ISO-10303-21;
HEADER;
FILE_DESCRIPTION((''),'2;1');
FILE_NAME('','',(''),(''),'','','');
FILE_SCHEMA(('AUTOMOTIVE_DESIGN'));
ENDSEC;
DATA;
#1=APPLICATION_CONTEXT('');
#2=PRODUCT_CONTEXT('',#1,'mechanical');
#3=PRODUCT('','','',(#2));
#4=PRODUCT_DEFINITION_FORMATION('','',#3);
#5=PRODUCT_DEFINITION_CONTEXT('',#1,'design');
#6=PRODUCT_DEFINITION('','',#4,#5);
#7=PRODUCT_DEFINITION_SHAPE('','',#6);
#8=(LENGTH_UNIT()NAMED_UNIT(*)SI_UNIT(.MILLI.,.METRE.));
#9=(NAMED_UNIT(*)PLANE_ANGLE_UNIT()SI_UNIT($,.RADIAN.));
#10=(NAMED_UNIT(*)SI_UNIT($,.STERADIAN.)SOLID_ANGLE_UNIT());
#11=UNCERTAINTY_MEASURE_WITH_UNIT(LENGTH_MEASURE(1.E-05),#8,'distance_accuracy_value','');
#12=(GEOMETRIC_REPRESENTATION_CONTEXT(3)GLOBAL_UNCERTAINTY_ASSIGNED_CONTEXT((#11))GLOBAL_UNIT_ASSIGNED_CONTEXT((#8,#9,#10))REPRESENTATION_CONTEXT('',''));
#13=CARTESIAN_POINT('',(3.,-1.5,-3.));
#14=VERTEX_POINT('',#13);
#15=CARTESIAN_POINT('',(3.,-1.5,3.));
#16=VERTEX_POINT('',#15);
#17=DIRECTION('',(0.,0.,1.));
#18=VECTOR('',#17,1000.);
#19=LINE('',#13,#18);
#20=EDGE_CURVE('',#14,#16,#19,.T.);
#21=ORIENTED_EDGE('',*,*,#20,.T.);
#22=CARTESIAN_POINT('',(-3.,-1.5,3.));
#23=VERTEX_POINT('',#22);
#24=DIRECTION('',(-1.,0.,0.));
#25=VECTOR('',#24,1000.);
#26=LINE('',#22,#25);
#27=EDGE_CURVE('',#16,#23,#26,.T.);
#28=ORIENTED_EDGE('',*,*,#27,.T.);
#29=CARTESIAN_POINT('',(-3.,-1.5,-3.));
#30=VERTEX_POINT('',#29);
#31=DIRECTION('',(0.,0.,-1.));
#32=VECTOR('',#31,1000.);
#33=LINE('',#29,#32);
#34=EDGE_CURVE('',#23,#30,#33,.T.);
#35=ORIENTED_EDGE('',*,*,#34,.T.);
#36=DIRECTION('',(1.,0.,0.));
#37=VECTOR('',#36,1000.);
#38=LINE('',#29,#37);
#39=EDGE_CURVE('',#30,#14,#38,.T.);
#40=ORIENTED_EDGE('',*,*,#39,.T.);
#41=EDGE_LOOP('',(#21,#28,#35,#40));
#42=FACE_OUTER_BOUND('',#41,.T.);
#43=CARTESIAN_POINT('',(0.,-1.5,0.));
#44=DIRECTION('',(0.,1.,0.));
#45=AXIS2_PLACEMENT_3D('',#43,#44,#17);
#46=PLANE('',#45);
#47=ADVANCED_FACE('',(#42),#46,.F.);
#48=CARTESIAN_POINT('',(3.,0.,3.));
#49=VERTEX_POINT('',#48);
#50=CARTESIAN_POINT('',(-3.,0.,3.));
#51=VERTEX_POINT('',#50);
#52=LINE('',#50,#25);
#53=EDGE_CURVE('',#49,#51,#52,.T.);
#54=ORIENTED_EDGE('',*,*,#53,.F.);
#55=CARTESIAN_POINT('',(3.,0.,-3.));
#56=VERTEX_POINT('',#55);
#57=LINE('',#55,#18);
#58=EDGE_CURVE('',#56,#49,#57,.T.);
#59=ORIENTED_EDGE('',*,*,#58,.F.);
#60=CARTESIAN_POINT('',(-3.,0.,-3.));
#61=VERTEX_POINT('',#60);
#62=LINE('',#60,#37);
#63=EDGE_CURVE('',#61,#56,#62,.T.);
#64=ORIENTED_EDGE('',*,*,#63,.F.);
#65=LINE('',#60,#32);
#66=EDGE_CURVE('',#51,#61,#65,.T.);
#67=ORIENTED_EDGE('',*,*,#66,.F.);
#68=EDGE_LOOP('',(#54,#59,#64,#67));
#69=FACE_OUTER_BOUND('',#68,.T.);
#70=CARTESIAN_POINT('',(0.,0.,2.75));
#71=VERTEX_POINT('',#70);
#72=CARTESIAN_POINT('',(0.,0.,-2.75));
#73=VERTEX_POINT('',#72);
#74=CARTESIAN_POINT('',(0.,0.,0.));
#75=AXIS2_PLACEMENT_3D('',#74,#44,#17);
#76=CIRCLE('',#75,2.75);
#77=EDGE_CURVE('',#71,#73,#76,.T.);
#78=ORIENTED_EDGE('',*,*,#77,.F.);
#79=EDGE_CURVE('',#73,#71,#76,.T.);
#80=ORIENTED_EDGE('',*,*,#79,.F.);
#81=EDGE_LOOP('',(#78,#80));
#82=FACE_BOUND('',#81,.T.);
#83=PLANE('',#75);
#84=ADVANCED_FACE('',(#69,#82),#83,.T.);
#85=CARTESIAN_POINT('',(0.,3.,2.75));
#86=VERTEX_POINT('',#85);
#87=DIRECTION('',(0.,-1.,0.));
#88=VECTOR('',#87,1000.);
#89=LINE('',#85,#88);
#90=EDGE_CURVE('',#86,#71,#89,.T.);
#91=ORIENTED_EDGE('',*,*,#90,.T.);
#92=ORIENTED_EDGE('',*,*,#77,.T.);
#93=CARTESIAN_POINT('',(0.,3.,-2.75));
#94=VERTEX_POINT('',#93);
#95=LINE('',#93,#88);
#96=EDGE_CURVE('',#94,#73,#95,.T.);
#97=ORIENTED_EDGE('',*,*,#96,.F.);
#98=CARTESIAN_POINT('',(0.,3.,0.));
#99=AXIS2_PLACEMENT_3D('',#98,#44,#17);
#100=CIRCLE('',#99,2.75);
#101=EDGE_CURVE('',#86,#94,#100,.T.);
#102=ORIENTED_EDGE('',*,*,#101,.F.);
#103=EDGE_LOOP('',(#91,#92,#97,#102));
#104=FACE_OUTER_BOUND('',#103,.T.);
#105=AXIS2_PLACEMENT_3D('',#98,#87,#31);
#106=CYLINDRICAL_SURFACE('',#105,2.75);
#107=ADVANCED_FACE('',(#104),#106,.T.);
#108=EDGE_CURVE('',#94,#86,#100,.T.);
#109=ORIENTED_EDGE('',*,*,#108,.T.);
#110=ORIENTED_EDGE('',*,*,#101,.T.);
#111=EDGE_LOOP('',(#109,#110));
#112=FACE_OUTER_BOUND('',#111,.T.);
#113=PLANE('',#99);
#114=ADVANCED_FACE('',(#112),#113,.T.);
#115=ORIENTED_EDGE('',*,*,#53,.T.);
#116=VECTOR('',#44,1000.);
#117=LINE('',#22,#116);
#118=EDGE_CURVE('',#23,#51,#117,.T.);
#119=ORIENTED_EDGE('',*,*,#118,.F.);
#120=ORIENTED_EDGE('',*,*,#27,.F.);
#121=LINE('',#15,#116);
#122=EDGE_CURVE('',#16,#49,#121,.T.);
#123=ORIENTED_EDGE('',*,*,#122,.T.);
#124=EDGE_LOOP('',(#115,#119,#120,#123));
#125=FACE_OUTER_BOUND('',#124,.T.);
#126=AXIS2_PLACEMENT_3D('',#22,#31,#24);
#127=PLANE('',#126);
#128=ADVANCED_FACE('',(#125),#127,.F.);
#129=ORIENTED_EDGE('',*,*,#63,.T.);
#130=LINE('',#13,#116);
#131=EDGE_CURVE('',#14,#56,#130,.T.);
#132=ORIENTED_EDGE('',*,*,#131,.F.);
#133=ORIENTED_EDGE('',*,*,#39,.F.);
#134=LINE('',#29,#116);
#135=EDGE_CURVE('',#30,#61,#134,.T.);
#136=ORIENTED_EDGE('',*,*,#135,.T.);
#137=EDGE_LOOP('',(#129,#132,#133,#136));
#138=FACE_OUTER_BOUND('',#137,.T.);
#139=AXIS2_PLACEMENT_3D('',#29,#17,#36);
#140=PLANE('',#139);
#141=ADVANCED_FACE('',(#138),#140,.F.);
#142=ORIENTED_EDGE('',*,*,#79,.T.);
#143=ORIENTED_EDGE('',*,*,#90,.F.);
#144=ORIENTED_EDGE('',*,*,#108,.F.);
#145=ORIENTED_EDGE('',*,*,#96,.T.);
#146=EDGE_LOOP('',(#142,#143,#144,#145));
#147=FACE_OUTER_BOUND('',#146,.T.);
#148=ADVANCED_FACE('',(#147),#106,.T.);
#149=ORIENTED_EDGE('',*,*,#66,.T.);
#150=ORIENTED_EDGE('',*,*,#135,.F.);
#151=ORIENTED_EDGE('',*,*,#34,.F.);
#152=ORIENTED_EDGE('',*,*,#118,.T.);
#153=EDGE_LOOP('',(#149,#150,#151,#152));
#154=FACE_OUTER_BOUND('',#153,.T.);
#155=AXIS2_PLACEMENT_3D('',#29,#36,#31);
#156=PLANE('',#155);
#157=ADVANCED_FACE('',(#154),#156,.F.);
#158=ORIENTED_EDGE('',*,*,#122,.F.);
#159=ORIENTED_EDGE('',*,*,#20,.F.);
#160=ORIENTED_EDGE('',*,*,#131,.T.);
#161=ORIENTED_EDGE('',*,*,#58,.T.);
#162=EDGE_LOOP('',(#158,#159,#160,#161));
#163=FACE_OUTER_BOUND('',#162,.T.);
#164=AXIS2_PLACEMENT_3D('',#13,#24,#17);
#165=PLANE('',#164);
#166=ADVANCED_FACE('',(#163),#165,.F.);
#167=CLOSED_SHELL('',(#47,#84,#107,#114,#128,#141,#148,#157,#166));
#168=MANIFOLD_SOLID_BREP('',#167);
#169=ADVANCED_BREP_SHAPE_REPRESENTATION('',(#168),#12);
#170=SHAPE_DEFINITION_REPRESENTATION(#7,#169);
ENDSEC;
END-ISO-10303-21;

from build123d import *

# Parameters (mm, degrees)
SKETCH1_R           = 2.75
BOSS_EXTRUDE1_DEPTH = 3
SKETCH2_W           = 6
SKETCH2_H           = 6
BOSS_EXTRUDE2_DEPTH = 1.5


with BuildPart() as part:
    # Sketch1 → Boss-Extrude1 (new body)
    with BuildSketch(Plane(origin=(0, 0, 0), x_dir=(1, 0, 0), z_dir=(0, 1, 0))):
        with Locations(Location((0, 0, 0), (0, 0, 270))):
            Circle(SKETCH1_R)
    extrude(amount=BOSS_EXTRUDE1_DEPTH)

    # Sketch2 → Boss-Extrude2 (add)
    with BuildSketch(Plane.XZ):
        Rectangle(SKETCH2_W, SKETCH2_H)
    extrude(amount=BOSS_EXTRUDE2_DEPTH)


solid = part.part
